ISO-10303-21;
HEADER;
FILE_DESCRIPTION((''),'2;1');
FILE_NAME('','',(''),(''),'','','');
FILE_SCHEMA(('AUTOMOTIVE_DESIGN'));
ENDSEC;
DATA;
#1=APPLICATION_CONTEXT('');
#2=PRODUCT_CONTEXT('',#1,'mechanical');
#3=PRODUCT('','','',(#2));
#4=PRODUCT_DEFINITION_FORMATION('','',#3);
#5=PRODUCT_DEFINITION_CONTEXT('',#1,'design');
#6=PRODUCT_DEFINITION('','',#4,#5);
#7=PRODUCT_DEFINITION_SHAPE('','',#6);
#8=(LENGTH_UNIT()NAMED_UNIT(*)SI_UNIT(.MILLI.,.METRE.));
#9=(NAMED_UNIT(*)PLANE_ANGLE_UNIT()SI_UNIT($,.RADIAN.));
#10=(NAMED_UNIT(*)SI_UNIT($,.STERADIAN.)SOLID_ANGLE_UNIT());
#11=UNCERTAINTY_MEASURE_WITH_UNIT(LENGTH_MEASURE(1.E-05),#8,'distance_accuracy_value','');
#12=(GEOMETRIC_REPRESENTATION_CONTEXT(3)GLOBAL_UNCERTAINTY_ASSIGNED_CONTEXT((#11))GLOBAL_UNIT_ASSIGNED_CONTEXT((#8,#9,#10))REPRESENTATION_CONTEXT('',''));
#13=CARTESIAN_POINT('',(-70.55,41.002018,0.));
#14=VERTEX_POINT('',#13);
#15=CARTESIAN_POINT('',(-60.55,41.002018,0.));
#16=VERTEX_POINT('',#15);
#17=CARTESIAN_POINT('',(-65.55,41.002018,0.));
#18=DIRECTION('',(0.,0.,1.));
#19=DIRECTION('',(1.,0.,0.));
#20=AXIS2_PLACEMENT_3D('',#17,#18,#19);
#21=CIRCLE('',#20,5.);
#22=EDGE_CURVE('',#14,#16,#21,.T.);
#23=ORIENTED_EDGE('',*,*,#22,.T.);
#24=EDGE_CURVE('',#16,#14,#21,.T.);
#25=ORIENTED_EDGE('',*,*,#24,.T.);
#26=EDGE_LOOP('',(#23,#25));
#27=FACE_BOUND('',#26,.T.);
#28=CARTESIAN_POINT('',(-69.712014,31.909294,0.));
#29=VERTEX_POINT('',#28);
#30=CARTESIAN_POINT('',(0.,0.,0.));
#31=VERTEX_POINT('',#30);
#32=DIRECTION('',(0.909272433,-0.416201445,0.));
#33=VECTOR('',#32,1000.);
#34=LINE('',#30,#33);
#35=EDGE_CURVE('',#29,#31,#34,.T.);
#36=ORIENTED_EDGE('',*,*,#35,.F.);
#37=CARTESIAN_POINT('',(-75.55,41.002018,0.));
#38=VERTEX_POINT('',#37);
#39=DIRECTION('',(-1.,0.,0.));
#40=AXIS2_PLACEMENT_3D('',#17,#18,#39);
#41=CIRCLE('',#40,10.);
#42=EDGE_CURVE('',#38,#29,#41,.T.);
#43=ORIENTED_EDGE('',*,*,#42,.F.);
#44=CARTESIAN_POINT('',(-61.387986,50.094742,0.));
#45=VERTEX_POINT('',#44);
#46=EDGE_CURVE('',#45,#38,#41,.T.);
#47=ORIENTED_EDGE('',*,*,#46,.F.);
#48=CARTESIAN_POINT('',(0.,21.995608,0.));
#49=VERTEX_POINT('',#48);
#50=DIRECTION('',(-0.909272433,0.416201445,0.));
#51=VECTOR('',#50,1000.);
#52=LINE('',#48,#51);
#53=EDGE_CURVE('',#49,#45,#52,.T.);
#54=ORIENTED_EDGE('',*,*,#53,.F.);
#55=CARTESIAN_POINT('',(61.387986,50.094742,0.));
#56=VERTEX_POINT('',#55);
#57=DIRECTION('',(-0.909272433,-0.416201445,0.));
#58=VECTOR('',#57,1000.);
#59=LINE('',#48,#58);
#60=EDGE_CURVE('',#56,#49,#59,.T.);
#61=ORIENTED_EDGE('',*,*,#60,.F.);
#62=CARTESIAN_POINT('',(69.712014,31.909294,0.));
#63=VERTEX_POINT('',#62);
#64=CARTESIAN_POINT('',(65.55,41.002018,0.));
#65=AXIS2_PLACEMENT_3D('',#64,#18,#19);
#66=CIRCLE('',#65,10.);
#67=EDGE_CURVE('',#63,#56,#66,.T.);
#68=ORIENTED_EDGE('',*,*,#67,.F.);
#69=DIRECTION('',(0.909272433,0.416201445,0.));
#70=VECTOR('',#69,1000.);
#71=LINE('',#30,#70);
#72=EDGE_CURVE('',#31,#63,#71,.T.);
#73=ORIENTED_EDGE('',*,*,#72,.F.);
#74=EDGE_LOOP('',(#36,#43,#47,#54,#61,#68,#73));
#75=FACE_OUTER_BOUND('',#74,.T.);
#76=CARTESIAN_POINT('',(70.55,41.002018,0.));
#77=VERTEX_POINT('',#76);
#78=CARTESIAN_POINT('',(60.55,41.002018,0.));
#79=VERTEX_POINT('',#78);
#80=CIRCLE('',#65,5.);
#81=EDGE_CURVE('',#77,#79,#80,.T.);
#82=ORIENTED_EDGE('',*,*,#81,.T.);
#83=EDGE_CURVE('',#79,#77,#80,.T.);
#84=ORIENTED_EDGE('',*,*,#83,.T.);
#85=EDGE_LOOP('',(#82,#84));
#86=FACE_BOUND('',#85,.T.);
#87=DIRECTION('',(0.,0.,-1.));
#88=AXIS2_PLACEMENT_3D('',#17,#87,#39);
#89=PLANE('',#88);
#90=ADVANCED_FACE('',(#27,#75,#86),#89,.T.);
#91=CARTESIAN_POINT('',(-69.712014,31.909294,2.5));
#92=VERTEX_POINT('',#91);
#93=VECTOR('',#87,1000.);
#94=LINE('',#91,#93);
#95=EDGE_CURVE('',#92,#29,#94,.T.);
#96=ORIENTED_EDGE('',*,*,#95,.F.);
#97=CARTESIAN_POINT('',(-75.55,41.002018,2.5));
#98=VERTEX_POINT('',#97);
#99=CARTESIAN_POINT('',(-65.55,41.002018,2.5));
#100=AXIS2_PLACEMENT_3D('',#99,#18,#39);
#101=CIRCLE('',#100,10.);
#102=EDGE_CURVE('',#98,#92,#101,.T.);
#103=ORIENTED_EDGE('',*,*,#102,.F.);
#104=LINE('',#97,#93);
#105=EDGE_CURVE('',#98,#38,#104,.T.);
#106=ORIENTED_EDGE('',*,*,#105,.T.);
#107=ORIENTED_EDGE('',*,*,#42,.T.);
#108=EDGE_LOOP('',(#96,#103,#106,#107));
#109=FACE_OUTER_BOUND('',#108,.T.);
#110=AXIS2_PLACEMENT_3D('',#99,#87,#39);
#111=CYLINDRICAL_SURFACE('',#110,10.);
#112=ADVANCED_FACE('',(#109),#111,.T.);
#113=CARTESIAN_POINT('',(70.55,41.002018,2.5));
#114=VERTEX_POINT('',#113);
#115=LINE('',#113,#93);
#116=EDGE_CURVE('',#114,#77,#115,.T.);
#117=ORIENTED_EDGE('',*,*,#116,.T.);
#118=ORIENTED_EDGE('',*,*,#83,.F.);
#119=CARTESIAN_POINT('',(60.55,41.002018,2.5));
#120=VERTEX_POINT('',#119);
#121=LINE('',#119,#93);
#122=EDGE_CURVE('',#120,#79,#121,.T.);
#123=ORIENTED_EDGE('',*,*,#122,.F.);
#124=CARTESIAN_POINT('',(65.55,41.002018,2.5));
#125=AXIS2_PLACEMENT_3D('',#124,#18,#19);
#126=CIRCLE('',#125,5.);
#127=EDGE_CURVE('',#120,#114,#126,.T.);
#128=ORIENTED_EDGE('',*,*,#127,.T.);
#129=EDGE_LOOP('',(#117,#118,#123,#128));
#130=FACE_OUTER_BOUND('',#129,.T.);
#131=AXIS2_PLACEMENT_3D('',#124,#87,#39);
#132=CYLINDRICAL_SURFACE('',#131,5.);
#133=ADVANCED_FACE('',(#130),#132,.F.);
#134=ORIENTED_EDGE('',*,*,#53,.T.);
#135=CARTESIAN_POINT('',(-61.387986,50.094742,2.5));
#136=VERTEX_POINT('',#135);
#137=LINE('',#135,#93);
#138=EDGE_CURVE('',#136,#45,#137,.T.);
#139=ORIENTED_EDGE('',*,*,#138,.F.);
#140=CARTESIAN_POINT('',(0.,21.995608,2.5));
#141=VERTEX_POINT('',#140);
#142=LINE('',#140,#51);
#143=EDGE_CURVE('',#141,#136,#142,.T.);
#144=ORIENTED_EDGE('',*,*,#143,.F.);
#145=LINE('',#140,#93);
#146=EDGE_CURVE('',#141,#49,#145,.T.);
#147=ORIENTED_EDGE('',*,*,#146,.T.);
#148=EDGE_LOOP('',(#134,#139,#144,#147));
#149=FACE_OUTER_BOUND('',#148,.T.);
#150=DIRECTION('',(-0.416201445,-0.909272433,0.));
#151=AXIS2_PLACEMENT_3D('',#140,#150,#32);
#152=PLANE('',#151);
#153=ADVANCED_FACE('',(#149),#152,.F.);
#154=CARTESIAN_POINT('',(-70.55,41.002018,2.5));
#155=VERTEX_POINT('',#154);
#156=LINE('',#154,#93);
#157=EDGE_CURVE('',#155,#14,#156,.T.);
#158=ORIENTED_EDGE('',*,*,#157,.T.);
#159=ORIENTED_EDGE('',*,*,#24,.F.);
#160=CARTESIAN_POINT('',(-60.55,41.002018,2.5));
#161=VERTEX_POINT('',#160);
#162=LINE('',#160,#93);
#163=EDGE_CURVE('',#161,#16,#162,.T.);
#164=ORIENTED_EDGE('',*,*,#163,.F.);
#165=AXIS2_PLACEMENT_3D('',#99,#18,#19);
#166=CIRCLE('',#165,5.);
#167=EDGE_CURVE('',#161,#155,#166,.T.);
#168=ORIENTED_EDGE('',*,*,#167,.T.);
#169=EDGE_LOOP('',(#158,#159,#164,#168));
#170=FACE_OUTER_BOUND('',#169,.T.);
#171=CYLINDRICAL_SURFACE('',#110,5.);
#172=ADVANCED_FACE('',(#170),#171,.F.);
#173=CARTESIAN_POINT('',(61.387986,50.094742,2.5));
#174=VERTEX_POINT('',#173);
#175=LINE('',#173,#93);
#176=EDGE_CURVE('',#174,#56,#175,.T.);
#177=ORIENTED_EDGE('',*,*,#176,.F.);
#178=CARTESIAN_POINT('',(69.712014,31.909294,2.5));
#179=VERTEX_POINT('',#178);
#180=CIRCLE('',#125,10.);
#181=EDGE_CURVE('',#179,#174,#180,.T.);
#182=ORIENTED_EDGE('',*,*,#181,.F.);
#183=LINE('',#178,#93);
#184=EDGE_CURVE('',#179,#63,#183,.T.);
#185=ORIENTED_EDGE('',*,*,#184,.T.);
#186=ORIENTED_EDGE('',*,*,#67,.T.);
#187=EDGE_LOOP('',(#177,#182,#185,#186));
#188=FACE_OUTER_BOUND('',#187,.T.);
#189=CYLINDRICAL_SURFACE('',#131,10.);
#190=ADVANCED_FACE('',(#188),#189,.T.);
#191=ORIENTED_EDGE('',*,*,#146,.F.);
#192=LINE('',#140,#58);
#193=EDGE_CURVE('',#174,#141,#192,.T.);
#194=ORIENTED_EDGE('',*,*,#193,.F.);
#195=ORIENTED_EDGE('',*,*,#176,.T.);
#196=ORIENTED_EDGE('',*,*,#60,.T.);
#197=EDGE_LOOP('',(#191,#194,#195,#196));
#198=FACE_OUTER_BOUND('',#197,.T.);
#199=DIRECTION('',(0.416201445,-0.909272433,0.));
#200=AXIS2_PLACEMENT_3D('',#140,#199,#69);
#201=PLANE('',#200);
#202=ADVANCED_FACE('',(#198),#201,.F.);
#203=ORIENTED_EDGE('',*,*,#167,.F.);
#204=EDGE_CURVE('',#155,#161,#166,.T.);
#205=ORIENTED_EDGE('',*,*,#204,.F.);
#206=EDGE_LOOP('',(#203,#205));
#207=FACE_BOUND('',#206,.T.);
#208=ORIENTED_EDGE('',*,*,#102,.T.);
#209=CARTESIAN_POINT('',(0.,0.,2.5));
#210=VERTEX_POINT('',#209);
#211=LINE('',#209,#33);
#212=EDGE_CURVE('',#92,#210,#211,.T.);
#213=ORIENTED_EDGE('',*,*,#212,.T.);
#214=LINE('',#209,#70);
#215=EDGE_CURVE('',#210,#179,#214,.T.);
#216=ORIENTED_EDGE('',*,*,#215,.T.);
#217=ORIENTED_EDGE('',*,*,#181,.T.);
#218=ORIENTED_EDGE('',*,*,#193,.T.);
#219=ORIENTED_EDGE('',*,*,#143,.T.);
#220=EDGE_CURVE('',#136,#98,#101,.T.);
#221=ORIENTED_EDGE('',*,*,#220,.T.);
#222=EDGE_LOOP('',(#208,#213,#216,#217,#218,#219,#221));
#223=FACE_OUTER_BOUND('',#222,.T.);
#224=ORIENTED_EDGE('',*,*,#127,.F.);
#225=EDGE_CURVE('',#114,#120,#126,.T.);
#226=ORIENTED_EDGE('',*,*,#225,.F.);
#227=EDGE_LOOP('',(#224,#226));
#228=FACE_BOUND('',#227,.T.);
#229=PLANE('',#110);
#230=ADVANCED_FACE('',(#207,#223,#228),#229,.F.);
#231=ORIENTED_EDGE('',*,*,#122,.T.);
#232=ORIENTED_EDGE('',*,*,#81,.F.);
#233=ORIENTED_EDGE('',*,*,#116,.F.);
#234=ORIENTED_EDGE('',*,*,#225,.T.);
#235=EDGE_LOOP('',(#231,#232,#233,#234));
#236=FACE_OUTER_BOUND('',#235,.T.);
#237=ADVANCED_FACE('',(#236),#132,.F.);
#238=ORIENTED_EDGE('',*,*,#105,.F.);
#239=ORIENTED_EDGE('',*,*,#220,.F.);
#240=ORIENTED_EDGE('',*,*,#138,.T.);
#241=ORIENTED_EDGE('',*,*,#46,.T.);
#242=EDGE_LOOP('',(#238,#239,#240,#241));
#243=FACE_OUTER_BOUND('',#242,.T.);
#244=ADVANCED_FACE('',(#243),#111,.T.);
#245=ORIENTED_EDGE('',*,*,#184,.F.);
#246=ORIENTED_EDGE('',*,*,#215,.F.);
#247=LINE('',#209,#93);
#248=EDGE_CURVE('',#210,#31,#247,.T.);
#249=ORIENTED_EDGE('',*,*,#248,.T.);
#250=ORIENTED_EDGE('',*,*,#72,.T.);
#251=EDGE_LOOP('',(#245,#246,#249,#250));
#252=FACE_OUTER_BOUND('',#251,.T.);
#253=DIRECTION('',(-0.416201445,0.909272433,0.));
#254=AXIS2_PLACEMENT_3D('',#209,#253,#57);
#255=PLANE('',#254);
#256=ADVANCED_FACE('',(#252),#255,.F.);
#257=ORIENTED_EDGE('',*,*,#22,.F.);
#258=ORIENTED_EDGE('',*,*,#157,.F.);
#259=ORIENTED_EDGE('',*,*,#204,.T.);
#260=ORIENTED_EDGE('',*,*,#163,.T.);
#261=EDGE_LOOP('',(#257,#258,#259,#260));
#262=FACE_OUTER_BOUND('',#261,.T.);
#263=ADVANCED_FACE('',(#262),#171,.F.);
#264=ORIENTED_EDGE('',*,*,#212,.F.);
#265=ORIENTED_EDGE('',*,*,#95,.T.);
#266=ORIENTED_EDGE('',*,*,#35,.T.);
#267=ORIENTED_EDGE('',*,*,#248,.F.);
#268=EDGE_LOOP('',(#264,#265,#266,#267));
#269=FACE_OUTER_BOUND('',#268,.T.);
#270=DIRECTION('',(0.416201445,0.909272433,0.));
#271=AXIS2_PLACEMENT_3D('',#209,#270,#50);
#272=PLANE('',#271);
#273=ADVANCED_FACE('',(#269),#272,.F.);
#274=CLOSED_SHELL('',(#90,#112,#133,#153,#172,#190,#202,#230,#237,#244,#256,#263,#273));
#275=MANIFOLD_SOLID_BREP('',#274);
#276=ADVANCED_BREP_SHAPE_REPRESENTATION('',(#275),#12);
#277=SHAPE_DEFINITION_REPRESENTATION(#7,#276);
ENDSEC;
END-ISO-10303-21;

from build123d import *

# Parameters (mm, degrees)
SKETCH1_R           = 5
BOSS_EXTRUDE1_DEPTH = 2.5


with BuildPart() as part:
    # Sketch1 → Boss-Extrude1 (new body)
    with BuildSketch(Plane.XY):
        with BuildLine():
            Line((0, 21.995608), (61.387985551, 50.094742382))
            ThreePointArc((61.387985551, 50.094742382), (74.642724329, 45.164032502), (69.712014449, 31.909293724))
            Line((69.712014449, 31.909293724), (0, 0))
            Line((0, 0), (-69.712014449, 31.909293724))
            ThreePointArc((-69.712014449, 31.909293724), (-74.642724329, 45.164032502), (-61.387985551, 50.094742382))
            Line((-61.387985551, 50.094742382), (0, 21.995608))
        make_face()
        with Locations((-65.55, 41.002018053)):
            Circle(SKETCH1_R, mode=Mode.SUBTRACT)
        with Locations((65.55, 41.002018053)):
            Circle(SKETCH1_R, mode=Mode.SUBTRACT)
    extrude(amount=BOSS_EXTRUDE1_DEPTH)


solid = part.part
